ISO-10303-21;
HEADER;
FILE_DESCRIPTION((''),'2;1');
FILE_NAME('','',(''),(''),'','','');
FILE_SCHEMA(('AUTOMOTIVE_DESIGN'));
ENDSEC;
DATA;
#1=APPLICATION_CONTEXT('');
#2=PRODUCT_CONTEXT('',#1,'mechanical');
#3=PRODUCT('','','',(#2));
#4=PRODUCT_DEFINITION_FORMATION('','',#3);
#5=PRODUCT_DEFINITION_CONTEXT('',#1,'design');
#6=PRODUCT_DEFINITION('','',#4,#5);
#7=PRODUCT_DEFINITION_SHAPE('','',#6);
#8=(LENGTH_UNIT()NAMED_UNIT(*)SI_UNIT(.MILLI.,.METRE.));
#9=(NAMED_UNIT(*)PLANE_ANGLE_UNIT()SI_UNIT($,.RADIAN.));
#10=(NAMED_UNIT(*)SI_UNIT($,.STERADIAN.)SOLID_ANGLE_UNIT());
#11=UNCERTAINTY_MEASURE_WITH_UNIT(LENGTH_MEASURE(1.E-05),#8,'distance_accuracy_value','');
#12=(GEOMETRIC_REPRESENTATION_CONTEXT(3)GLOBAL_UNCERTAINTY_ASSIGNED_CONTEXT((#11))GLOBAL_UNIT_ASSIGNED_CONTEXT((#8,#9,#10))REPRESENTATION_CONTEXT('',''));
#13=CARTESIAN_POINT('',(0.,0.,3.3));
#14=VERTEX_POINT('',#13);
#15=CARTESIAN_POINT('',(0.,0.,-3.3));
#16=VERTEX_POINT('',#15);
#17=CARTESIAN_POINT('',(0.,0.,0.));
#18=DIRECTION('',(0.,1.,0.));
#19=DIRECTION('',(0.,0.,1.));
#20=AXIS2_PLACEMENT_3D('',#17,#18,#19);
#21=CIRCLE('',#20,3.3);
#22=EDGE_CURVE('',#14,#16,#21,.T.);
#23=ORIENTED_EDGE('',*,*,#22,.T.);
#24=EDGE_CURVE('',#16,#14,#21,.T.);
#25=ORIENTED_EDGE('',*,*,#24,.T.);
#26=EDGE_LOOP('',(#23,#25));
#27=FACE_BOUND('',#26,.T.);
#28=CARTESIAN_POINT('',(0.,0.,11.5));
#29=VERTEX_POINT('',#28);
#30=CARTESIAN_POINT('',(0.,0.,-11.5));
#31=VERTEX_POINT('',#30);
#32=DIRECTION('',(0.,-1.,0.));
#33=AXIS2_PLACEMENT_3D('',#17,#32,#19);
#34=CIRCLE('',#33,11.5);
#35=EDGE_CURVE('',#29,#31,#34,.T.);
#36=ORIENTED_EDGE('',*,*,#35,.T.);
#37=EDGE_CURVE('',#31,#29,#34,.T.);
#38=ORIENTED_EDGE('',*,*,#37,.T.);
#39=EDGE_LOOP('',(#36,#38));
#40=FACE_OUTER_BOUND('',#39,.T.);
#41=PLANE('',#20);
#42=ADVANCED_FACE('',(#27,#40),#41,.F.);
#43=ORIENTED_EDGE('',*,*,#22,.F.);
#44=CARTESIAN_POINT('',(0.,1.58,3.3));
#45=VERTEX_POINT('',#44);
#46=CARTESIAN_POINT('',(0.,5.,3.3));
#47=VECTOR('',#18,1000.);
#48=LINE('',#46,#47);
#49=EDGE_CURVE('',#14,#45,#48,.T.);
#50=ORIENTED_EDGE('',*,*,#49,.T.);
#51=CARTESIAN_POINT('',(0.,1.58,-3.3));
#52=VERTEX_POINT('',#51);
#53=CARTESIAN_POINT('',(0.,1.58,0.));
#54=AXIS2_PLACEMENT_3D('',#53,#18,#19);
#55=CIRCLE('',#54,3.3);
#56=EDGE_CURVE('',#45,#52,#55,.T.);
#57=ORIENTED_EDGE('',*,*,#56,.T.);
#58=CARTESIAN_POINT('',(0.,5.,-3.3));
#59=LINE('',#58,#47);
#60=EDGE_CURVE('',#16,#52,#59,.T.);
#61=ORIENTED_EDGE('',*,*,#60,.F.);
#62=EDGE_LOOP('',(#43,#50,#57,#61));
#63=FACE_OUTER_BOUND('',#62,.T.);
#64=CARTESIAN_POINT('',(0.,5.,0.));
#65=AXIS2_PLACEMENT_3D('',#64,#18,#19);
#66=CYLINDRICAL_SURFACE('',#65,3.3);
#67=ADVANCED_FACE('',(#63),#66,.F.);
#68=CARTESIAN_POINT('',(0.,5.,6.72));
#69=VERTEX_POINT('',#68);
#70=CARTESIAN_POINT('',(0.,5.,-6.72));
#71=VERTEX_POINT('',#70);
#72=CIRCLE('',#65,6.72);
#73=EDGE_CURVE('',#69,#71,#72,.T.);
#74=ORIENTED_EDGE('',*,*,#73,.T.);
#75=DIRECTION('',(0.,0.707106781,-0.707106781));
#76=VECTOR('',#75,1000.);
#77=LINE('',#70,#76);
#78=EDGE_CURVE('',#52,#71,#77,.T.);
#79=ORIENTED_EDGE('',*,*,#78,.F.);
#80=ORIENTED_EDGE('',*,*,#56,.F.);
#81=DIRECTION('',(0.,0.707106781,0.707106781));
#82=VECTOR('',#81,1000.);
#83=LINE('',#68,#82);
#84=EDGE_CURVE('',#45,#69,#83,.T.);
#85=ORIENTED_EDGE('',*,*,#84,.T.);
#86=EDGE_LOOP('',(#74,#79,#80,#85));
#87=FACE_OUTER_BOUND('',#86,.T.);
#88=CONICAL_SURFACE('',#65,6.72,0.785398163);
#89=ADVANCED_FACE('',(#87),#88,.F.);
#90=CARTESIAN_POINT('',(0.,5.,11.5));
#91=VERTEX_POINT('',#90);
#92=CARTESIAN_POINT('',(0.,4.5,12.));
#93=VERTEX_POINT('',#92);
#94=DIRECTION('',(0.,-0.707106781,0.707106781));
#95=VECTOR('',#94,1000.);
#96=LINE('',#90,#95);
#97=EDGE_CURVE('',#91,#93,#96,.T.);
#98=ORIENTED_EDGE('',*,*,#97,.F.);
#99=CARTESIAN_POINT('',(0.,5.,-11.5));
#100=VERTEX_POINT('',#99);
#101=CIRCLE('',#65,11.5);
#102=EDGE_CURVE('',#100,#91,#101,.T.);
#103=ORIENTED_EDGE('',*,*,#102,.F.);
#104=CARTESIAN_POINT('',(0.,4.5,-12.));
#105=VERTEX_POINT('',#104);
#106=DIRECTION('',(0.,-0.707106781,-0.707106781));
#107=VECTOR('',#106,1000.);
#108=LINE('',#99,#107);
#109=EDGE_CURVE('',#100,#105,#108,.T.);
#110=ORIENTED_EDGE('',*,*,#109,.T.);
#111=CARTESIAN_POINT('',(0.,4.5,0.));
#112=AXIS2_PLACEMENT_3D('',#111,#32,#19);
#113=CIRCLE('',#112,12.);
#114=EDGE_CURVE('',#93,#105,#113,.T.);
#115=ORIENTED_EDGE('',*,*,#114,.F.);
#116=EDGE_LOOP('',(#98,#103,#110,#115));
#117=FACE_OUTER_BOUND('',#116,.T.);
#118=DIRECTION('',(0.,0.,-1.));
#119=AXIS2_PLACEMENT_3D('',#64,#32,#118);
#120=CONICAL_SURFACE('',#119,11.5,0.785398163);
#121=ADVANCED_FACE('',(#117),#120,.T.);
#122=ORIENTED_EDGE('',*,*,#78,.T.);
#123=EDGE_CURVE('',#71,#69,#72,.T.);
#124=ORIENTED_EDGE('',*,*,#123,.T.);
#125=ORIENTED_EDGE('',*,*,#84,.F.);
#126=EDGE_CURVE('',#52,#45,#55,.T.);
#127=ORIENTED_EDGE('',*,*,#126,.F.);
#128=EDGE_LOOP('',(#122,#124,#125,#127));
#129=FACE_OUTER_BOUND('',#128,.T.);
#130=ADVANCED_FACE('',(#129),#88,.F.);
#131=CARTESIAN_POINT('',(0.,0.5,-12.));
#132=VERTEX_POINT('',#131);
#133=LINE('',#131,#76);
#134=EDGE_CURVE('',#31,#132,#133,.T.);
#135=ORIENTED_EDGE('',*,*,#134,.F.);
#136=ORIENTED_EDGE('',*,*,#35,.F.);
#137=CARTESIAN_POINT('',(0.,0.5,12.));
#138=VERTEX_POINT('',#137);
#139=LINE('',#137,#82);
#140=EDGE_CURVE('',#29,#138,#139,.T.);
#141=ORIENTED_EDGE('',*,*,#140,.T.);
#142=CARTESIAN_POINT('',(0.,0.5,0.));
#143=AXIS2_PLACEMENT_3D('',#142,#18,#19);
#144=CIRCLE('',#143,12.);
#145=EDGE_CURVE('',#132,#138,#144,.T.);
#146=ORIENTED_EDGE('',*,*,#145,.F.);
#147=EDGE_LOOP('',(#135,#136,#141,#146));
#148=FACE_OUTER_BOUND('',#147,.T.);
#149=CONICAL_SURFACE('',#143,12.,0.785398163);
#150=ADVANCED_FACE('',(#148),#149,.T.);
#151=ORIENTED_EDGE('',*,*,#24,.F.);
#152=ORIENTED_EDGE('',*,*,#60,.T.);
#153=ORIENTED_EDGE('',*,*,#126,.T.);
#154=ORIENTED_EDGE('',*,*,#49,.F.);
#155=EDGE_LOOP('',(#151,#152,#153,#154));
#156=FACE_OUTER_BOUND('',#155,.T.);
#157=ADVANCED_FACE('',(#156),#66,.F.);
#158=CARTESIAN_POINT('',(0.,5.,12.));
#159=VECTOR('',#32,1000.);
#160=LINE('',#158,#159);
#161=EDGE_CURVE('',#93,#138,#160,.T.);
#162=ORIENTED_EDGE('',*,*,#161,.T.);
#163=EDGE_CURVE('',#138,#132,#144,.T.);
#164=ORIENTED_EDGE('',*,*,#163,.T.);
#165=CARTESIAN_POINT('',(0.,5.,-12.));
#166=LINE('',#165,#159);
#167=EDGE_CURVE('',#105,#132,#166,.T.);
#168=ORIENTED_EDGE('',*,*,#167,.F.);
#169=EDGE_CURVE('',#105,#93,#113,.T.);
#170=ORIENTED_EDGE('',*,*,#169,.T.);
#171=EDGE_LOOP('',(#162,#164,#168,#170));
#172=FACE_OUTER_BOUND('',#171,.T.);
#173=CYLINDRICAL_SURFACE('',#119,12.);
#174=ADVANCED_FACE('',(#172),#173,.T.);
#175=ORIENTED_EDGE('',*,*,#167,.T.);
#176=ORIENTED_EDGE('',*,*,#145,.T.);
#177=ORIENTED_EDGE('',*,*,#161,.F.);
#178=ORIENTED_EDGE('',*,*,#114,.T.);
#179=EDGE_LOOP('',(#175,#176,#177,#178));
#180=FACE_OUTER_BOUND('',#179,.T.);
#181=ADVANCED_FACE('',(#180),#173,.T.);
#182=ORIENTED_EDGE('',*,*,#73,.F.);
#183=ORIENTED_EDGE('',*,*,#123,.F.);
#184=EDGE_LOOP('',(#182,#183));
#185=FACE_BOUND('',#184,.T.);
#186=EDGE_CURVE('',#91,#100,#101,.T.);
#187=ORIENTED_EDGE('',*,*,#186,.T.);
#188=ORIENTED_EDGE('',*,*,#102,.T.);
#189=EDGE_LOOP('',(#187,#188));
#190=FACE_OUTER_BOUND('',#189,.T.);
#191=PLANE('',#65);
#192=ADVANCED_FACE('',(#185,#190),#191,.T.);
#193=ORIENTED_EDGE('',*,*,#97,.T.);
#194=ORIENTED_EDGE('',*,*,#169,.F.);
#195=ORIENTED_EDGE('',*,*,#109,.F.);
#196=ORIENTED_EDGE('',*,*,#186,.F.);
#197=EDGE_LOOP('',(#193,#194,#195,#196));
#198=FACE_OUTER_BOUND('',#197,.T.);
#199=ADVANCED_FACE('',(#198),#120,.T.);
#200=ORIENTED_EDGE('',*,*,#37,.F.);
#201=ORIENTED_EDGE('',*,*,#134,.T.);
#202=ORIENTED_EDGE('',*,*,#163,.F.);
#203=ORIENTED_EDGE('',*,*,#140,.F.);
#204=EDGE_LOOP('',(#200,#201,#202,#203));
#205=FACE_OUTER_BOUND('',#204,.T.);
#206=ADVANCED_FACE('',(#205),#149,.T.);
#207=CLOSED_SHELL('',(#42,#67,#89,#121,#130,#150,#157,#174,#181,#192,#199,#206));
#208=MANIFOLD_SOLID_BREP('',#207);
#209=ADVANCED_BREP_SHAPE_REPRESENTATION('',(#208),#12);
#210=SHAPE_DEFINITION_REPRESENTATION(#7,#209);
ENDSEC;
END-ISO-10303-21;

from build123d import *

# Parameters (mm, degrees)
SKETCH_1_R      = 12
EXTRUDE_1_DEPTH = 5
CHAMFER_1_SIZE  = 0.5


with BuildPart() as part:
    # 草图1 → 凸台-拉伸1 (new body)
    with BuildSketch(Plane(origin=(0, 0, 0), x_dir=(1, 0, 0), z_dir=(0, 1, 0))):
        with Locations(Location((0, 0, 0), (0, 0, 270))):
            Circle(SKETCH_1_R)
    extrude(amount=EXTRUDE_1_DEPTH)

    # 草图2 → M6 六角凹锥坑螺钉的锥形沉头孔1 (revolve, cut)
    with BuildSketch(Plane(origin=(0, 5, 0), x_dir=(0, 0, 1), z_dir=(1, 0, 0))):
        Polygon((0, 0), (0, 5), (3.3, 5), (3.3, 3.42), (6.72, 0), align=None)
    revolve(axis=Axis((0, 11.35, 0), (0, -1, 0)), mode=Mode.SUBTRACT)

    # 倒角1
    chamfer_1_edges = [part.edges().sort_by_distance(p)[0] for p in [
        (0, 0, -12),
        (0, 5, -12),
    ]]
    chamfer(chamfer_1_edges, length=CHAMFER_1_SIZE)


solid = part.part
